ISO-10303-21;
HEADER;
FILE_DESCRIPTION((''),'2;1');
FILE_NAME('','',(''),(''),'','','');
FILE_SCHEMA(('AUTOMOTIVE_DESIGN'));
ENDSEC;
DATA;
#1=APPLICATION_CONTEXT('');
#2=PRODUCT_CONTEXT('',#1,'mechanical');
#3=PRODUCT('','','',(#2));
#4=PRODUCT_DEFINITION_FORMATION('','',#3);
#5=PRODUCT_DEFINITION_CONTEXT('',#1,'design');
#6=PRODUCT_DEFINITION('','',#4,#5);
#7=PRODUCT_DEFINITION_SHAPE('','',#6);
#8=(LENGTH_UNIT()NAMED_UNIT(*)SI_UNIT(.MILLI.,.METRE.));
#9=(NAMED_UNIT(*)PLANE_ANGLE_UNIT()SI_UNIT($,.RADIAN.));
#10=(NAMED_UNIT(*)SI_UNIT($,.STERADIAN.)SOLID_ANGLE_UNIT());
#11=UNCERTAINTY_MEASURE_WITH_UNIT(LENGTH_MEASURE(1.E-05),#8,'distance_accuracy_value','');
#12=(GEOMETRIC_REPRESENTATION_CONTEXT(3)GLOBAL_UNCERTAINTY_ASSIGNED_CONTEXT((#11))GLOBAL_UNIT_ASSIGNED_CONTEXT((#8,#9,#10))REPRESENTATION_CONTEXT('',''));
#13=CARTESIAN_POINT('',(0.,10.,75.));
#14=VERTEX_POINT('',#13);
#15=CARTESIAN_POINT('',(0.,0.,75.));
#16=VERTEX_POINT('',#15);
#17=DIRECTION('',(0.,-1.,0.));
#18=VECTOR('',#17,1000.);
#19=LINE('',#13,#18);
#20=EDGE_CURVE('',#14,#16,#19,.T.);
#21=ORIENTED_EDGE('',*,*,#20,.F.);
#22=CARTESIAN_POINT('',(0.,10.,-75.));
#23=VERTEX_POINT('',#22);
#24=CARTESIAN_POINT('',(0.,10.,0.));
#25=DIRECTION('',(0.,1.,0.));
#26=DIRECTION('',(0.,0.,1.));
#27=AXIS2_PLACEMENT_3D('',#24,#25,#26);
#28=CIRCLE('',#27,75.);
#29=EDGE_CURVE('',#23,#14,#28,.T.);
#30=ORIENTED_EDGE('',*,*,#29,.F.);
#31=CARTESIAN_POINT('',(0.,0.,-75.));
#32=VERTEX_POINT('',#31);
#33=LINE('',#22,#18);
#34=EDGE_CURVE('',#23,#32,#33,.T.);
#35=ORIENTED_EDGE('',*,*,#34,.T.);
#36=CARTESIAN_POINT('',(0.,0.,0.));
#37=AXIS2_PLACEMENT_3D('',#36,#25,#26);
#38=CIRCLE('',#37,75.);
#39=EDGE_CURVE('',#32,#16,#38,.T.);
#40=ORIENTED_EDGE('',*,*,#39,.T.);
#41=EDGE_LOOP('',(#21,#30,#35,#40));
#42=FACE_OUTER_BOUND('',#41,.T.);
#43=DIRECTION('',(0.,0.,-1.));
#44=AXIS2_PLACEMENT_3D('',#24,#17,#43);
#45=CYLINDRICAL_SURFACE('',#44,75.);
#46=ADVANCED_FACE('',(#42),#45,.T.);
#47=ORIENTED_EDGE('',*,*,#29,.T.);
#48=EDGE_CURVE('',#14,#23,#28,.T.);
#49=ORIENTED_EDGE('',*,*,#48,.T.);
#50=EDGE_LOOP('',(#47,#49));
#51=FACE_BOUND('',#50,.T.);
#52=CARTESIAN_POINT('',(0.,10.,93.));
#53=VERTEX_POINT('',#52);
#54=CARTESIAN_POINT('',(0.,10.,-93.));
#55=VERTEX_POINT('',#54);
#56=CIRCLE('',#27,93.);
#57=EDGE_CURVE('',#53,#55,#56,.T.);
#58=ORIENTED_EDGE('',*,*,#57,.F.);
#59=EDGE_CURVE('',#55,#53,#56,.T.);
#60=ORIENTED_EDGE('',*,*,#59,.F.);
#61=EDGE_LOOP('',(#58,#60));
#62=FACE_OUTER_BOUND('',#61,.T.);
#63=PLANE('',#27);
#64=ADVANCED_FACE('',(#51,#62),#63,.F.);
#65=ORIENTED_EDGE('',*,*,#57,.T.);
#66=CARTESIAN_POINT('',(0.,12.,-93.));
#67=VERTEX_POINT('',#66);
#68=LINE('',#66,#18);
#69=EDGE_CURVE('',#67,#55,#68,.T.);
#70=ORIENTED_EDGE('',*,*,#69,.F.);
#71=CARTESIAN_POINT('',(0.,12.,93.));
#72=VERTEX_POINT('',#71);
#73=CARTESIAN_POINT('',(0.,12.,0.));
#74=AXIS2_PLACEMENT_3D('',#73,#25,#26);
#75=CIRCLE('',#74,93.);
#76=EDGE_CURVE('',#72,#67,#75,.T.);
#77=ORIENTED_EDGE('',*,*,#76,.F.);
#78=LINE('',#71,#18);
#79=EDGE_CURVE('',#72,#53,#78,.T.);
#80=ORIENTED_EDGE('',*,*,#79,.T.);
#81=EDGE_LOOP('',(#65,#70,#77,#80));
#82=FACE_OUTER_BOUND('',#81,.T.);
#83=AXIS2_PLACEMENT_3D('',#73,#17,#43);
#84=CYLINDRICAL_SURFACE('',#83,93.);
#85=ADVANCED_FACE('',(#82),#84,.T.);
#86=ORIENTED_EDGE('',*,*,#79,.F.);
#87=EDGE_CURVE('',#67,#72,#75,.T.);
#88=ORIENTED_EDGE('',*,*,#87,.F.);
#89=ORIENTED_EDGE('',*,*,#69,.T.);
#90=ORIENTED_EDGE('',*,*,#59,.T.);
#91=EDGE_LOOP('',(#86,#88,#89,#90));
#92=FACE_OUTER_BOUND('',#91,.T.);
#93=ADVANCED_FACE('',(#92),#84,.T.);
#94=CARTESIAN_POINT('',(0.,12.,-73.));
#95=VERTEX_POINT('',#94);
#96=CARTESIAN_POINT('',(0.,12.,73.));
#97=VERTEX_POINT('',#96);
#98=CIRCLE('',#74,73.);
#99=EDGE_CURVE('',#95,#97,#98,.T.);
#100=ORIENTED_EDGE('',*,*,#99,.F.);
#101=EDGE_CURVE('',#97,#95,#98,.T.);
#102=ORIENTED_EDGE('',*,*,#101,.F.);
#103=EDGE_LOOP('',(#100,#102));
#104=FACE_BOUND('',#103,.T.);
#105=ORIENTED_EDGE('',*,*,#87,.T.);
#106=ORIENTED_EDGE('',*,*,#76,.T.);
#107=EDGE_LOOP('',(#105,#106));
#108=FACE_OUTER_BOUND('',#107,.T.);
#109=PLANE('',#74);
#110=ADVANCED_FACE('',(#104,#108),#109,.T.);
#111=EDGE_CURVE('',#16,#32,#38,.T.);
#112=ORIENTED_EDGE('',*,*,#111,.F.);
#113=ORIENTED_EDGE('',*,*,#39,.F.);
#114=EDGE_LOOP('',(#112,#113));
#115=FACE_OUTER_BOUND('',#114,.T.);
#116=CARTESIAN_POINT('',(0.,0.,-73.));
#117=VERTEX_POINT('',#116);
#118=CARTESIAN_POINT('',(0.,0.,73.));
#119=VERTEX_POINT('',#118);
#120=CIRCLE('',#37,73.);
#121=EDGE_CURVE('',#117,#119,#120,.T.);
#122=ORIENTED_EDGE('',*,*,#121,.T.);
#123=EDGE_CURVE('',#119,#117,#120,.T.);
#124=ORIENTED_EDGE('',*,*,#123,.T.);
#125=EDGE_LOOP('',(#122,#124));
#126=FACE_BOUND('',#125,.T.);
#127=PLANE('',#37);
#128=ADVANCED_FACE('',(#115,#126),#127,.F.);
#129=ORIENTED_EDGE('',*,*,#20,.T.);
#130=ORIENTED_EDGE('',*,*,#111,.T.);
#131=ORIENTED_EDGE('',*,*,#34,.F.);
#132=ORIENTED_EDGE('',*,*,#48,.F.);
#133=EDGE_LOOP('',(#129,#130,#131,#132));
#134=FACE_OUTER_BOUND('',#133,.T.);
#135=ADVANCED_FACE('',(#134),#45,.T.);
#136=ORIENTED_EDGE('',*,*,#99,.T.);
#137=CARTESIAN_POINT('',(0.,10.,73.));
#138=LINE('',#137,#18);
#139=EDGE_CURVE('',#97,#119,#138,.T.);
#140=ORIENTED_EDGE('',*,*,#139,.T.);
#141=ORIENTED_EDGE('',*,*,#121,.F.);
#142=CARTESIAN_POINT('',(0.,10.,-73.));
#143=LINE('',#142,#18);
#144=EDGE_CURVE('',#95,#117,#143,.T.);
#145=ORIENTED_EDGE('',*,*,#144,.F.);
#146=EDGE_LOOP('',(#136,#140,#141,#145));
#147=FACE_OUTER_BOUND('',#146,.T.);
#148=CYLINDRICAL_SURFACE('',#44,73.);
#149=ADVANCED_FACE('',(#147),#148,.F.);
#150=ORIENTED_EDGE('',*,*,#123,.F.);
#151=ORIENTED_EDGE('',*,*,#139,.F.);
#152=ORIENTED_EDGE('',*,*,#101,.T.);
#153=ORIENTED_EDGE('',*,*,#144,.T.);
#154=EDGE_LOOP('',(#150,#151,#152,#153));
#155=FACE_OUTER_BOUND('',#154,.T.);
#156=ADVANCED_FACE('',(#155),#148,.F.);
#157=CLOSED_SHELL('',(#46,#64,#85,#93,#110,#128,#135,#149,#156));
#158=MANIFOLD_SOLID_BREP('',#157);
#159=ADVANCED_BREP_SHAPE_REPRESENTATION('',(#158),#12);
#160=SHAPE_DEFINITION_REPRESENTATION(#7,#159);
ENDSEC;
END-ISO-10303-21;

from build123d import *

# Parameters (mm, degrees)
SKETCH1_R           = 75
SKETCH1_R_2         = 73
BOSS_EXTRUDE1_DEPTH = 10
SKETCH3_R           = 93
SKETCH3_R_2         = 73
BOSS_EXTRUDE2_DEPTH = 2


with BuildPart() as part:
    # Sketch1 → Boss-Extrude1 (new body)
    with BuildSketch(Plane(origin=(0, 0, 0), x_dir=(1, 0, 0), z_dir=(0, 1, 0))):
        with Locations(Location((0, 0, 0), (0, 0, 270))):
            Circle(SKETCH1_R)
        with Locations(Location((0, 0, 0), (0, 0, 270))):
            Circle(SKETCH1_R_2, mode=Mode.SUBTRACT)
    extrude(amount=BOSS_EXTRUDE1_DEPTH)

    # Sketch3 → Boss-Extrude2 (add)
    with BuildSketch(Plane(origin=(0, 10, 0), x_dir=(1, 0, 0), z_dir=(0, 1, 0))):
        with Locations(Location((0, 0, 0), (0, 0, 270))):
            Circle(SKETCH3_R)
        with Locations(Location((0, 0, 0), (0, 0, 270))):
            Circle(SKETCH3_R_2, mode=Mode.SUBTRACT)
    extrude(amount=BOSS_EXTRUDE2_DEPTH)


solid = part.part
